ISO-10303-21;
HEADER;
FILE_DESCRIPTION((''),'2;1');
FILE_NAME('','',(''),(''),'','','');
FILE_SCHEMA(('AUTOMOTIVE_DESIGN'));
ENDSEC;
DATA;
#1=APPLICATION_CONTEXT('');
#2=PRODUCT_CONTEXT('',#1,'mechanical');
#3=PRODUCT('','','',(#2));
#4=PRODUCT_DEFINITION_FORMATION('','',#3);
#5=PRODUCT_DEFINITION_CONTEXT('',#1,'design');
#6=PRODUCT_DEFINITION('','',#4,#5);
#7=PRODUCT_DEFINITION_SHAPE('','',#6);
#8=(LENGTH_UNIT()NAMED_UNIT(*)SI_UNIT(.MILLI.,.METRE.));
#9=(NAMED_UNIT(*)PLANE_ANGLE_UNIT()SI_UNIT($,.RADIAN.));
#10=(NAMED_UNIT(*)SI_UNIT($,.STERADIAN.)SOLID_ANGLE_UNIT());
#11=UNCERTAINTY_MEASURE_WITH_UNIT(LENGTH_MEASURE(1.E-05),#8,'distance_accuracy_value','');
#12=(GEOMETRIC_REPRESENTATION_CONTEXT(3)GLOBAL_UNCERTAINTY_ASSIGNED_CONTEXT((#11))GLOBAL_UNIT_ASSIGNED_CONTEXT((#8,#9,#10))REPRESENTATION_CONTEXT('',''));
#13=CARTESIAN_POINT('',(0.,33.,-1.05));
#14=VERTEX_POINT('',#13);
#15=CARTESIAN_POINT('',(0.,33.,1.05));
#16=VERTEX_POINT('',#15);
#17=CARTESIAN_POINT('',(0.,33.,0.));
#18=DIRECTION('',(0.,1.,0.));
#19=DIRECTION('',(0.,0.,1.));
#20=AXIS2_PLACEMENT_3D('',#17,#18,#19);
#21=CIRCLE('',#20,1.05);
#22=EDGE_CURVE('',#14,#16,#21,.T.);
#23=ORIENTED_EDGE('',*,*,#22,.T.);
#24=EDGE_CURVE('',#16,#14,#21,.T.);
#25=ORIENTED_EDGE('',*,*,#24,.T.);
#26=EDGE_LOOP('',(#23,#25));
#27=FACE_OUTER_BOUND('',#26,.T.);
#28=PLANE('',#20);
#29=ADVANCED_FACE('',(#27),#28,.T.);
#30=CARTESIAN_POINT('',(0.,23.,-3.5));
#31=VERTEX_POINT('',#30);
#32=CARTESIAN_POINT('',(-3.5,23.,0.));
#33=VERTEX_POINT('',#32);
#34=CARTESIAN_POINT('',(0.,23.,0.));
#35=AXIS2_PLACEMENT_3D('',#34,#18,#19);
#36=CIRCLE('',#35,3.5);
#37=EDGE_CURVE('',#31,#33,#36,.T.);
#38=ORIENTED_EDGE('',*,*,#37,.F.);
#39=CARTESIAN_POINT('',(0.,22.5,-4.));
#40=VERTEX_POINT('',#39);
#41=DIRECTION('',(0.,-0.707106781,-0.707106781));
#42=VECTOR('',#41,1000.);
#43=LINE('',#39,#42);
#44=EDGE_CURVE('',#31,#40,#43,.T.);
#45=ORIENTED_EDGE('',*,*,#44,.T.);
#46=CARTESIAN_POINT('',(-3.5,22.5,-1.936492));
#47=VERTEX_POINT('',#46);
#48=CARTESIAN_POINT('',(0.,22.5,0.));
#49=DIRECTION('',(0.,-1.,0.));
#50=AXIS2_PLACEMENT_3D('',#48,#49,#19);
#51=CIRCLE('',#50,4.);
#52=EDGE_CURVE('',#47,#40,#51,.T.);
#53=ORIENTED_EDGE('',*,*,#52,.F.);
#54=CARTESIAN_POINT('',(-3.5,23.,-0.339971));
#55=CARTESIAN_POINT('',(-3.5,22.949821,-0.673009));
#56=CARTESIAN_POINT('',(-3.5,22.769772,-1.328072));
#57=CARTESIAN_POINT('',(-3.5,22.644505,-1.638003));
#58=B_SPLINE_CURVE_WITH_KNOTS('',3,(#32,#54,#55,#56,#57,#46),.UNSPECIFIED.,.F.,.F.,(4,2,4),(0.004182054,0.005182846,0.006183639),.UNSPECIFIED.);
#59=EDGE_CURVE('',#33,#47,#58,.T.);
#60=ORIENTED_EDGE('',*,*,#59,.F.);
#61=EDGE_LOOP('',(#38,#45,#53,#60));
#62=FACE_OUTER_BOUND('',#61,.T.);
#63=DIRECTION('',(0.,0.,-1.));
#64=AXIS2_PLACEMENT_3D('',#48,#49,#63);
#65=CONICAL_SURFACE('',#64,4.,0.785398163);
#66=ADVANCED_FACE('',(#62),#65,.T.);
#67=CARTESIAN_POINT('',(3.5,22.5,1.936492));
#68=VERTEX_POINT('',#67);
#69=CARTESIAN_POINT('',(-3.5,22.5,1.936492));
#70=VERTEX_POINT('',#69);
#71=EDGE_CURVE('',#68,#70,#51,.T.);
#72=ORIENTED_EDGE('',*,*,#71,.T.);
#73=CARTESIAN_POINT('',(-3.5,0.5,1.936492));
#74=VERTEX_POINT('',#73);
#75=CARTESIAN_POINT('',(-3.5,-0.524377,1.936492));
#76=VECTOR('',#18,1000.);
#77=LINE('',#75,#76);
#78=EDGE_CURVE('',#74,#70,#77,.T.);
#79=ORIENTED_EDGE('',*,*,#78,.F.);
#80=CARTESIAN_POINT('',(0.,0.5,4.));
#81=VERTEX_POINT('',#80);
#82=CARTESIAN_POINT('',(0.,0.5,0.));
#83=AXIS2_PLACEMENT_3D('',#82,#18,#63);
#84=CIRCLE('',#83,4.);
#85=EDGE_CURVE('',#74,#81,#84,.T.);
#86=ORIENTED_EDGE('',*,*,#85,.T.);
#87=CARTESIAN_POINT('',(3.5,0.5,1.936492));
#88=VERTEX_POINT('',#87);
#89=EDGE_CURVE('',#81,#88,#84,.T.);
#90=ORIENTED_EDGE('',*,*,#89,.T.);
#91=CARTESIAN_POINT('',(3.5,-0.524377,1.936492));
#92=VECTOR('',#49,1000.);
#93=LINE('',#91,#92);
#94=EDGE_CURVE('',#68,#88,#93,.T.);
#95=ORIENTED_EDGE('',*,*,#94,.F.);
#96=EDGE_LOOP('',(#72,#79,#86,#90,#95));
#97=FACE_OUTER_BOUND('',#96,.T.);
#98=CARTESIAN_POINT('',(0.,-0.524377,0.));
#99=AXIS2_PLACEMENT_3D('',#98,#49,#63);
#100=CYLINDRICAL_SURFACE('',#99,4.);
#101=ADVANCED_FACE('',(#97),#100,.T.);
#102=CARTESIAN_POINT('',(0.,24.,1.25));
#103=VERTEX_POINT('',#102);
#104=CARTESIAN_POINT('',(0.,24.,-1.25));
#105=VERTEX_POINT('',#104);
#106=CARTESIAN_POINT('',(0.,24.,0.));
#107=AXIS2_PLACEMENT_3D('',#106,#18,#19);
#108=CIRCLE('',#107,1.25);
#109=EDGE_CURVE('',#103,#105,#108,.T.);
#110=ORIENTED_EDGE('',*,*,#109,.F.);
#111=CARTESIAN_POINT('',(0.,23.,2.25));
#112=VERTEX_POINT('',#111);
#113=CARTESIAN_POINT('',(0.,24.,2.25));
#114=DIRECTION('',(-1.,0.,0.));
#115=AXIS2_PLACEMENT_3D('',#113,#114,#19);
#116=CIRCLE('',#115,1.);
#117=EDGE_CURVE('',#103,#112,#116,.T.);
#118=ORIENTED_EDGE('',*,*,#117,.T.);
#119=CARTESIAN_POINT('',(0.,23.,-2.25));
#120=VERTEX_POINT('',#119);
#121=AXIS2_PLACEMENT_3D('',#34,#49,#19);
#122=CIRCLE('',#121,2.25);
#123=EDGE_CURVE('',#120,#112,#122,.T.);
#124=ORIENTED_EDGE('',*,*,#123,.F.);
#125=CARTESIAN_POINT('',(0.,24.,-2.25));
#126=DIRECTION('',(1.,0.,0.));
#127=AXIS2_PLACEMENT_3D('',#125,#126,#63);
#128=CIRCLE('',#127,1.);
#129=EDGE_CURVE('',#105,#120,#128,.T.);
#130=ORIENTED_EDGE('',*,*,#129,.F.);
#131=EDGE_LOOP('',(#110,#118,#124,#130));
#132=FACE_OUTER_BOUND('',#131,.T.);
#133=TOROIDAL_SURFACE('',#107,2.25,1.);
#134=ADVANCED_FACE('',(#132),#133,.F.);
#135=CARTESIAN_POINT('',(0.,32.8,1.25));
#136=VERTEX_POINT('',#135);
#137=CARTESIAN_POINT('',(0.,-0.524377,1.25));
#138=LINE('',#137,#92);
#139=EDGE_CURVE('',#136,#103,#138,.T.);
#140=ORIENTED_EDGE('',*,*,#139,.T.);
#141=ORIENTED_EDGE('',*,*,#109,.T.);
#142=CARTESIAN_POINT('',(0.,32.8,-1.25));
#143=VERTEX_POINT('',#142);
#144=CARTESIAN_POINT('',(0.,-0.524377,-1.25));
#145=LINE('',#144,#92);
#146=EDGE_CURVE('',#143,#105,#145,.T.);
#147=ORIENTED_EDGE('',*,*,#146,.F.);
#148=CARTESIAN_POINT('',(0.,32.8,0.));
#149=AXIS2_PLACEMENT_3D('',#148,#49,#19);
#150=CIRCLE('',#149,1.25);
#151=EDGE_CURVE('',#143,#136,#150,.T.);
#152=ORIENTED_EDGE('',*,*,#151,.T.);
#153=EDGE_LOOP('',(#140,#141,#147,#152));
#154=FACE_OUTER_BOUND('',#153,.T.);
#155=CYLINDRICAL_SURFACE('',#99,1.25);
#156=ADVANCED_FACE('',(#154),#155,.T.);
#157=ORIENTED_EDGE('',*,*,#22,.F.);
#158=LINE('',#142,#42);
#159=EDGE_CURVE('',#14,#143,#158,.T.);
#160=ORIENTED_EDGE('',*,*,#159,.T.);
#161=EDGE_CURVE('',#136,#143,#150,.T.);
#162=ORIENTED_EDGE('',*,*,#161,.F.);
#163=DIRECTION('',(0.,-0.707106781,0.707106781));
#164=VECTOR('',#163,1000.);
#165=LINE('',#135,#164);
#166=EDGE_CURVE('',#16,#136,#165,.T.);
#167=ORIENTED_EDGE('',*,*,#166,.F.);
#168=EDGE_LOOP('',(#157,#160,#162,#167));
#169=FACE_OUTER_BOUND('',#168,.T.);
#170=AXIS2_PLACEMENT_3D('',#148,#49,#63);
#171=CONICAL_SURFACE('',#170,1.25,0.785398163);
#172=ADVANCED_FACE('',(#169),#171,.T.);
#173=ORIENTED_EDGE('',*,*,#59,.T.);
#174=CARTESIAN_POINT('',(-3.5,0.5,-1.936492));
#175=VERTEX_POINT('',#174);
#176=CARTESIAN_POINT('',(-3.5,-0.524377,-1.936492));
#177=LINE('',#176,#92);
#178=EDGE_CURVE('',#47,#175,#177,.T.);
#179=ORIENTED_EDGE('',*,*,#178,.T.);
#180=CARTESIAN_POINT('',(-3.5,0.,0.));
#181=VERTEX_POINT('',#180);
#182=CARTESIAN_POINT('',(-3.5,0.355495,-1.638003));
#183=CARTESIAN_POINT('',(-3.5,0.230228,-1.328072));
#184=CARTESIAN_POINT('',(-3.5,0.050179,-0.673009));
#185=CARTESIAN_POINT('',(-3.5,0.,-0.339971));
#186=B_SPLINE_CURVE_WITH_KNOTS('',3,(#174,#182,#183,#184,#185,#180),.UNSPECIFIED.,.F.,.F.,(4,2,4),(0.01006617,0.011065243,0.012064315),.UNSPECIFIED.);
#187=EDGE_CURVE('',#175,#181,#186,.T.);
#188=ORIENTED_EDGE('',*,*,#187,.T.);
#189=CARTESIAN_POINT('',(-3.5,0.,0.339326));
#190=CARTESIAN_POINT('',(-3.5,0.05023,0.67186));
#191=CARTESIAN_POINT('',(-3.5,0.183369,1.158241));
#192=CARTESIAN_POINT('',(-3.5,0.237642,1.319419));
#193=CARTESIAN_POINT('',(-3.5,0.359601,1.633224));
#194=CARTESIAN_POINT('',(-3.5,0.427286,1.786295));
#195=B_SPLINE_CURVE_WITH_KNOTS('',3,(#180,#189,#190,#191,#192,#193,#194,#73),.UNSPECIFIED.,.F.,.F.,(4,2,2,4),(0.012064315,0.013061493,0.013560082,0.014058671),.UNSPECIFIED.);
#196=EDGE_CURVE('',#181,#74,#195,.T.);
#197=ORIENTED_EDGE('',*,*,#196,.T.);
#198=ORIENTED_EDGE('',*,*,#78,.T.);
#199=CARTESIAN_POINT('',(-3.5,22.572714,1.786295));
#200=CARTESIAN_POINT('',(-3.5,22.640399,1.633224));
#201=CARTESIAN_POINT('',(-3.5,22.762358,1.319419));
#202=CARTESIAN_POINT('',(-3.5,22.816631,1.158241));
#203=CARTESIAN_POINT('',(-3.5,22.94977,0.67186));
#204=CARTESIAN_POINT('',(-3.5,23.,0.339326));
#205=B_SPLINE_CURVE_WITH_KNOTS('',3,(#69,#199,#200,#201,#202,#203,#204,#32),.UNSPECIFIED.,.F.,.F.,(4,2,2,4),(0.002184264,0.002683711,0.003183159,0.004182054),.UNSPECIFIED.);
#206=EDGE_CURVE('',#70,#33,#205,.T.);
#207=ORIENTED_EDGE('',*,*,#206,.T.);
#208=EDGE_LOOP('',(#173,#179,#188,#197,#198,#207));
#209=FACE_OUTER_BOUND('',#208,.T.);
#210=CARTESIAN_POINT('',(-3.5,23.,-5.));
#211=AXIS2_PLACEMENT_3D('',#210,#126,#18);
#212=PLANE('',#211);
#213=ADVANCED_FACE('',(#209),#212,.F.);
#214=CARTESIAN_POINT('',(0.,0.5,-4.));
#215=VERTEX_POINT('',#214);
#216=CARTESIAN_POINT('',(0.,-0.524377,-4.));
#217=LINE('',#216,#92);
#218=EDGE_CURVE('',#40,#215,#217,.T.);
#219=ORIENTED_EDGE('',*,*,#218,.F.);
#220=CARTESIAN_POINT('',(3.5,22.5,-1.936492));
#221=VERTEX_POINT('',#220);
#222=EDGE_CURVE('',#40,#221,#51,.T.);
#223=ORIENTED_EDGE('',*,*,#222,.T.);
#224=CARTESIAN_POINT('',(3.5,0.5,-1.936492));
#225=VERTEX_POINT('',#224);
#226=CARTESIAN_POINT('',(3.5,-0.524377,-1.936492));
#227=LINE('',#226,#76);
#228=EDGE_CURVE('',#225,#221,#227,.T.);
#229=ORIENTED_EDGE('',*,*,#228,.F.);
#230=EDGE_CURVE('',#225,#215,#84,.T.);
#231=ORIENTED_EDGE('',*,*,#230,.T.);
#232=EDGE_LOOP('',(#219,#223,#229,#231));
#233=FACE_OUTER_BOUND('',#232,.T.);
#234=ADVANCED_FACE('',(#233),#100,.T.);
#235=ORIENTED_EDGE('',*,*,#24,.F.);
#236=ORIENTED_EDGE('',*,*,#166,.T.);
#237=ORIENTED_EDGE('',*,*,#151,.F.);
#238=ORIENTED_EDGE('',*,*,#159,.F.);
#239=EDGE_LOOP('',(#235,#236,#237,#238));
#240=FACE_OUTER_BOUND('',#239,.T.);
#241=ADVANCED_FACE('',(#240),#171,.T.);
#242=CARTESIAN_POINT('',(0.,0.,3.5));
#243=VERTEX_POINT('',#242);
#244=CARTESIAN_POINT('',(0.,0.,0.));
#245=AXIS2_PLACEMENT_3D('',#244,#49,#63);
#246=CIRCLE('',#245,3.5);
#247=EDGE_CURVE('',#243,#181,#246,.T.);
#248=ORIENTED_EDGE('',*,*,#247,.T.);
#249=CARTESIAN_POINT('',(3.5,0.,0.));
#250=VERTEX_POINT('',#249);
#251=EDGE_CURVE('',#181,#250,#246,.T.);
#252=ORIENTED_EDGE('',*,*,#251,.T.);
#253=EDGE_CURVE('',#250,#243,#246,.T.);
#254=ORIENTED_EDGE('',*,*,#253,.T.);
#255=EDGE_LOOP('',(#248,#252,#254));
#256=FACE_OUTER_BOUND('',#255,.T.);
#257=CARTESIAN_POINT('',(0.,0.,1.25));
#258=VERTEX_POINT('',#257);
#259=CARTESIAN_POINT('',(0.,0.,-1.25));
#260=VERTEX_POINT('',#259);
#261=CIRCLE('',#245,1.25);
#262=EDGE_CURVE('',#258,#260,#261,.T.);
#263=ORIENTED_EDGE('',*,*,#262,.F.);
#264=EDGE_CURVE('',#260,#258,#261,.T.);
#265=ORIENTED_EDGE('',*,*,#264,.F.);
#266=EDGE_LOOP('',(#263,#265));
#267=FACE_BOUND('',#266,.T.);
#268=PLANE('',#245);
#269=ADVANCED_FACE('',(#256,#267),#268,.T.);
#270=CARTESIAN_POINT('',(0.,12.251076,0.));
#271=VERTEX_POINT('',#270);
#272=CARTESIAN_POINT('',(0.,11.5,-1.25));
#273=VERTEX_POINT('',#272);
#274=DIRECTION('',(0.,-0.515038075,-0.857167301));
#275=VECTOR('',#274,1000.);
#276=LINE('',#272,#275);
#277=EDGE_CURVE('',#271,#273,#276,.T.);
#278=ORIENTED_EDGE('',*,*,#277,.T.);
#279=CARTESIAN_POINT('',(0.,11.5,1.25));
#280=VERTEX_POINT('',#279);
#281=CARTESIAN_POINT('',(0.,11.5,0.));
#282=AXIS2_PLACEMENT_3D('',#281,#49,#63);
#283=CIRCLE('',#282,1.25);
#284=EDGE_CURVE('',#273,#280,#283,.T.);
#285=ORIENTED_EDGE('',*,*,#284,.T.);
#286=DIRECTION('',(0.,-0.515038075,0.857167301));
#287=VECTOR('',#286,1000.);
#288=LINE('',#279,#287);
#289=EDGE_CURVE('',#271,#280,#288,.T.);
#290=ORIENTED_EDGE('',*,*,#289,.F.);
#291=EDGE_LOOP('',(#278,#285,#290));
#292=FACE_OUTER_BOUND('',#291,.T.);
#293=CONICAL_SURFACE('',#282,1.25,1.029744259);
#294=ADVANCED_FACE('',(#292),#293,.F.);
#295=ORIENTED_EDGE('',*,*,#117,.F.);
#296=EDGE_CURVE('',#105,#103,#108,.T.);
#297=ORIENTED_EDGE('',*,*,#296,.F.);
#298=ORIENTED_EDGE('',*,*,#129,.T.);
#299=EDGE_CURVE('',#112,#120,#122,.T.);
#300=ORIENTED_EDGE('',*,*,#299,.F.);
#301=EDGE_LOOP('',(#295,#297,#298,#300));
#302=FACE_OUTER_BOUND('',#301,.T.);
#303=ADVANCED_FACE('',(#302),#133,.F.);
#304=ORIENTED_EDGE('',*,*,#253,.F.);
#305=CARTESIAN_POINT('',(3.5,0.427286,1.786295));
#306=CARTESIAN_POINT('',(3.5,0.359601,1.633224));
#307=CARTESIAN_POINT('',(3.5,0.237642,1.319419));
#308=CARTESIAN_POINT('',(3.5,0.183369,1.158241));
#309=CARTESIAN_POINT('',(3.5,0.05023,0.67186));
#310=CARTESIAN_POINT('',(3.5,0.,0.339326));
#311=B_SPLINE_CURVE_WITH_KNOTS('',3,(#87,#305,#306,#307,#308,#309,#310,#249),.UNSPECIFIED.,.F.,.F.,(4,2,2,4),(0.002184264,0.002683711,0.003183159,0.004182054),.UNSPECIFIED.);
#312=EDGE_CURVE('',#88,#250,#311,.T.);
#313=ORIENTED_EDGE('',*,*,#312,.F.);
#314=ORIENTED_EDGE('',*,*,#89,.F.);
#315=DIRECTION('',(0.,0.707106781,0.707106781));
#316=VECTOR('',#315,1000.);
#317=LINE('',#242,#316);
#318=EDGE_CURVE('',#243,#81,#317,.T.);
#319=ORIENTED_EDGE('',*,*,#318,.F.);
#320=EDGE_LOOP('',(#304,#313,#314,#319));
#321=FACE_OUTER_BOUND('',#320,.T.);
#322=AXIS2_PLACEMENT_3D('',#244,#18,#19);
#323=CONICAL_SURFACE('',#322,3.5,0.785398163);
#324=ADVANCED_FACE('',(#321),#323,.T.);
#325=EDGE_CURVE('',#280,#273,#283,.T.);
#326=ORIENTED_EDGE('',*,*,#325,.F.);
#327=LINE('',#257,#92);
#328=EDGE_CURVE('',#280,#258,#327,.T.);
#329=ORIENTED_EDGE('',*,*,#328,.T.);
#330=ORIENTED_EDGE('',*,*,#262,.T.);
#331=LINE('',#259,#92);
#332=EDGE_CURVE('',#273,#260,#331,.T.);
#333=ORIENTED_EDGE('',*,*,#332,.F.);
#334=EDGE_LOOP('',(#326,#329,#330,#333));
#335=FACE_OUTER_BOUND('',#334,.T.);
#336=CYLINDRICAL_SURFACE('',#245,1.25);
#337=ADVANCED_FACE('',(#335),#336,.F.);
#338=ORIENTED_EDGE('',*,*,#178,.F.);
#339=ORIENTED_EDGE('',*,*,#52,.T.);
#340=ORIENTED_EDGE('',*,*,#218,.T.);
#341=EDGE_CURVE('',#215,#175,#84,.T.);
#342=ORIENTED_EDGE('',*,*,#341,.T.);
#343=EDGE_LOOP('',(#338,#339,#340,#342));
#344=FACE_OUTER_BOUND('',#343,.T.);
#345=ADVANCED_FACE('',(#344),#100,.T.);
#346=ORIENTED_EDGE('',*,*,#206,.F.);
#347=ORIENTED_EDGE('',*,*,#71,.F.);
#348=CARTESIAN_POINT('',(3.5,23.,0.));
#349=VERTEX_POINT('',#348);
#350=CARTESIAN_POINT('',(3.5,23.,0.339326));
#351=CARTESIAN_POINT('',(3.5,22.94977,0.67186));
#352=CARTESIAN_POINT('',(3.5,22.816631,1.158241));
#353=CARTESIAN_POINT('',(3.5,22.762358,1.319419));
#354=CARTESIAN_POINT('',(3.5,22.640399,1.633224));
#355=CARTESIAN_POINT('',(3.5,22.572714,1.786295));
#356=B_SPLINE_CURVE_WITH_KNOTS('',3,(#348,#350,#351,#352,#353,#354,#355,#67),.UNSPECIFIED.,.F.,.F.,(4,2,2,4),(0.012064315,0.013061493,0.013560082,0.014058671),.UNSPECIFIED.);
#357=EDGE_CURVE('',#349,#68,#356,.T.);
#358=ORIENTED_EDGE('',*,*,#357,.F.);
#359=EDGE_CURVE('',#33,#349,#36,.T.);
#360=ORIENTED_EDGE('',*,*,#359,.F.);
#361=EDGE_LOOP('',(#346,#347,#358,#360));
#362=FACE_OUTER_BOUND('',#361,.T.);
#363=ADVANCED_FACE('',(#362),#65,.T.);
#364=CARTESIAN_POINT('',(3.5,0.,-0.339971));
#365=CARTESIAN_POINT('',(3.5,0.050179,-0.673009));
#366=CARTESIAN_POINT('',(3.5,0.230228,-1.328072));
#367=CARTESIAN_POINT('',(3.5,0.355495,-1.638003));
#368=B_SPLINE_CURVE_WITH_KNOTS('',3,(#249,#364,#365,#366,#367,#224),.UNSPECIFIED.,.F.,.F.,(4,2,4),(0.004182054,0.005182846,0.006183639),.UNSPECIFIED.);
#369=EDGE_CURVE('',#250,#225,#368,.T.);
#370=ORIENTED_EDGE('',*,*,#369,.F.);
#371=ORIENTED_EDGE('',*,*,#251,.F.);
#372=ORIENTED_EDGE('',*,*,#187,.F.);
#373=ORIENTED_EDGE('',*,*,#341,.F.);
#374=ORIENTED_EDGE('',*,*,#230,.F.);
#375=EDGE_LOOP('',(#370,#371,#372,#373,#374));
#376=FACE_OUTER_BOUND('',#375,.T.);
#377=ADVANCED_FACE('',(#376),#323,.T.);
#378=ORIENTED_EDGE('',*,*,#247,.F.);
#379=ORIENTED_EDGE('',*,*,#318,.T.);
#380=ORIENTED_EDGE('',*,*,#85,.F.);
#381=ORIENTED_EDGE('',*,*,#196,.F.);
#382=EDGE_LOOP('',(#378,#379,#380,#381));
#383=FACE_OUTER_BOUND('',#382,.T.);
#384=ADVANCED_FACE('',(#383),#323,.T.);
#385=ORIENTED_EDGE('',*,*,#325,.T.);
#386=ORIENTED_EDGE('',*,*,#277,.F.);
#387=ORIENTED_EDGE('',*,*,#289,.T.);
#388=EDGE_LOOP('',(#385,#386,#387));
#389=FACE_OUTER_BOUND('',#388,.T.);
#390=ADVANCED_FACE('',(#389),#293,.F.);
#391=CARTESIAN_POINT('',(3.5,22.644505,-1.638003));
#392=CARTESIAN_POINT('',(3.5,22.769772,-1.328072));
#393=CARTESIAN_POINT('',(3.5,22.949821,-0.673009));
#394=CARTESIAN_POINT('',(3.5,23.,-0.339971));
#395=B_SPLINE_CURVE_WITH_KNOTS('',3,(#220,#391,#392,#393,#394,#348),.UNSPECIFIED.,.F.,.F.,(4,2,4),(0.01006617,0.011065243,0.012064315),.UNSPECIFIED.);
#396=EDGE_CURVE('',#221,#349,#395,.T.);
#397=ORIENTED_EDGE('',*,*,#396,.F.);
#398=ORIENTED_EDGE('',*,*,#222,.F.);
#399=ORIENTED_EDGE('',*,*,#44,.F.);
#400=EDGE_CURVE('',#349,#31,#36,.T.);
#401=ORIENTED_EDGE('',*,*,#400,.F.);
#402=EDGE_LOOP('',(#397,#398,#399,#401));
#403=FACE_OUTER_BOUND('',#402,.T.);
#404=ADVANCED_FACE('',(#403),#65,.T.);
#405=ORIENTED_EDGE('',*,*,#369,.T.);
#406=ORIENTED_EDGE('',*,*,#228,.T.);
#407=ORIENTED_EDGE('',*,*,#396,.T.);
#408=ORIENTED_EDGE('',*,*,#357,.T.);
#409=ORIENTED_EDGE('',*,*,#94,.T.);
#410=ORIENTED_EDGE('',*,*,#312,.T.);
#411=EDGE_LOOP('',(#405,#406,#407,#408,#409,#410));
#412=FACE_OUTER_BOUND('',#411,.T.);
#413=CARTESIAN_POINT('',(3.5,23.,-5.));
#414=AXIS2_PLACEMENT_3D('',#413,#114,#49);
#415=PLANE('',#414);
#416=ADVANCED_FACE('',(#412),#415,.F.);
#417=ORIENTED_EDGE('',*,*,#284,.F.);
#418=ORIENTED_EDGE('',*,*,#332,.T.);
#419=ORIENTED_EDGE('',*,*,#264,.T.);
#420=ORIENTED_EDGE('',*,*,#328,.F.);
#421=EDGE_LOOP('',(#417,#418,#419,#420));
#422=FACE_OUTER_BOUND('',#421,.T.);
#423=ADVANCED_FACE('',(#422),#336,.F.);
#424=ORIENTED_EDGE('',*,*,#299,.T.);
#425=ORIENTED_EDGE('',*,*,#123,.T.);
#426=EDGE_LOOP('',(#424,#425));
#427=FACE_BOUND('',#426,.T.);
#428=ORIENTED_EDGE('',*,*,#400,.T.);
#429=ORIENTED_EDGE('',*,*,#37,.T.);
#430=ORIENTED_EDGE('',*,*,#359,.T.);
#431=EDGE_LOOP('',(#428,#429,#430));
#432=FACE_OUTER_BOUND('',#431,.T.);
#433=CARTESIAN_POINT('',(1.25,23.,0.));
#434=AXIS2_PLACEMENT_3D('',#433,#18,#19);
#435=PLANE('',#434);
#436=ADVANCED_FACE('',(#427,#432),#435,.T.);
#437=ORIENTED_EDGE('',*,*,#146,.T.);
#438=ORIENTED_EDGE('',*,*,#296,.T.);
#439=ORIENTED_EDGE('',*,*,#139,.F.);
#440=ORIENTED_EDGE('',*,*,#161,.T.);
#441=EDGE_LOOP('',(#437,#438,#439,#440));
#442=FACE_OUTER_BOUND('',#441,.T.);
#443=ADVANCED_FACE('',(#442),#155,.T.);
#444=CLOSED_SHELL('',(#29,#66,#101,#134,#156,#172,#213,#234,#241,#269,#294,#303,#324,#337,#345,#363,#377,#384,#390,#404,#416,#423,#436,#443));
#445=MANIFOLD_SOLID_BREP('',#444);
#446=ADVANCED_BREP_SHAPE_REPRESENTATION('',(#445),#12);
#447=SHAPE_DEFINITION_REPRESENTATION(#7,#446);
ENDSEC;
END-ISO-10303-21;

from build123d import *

# Parameters (mm, degrees)
HOLE_WIZARD_M3_1_D     = 2.5
HOLE_WIZARD_M3_1_DEPTH = 11.5
HOLE_WIZARD_M3_1_TIP   = 0.751075774
CHAMFER_1_SIZE         = 0.5
FILLET_1_R             = 1
SKETCH_4_W             = 0.5
SKETCH_4_H             = 23
CUT_EXTRUDE_1_DEPTH    = 5
CHAMFER_2_SIZE         = 0.2


with BuildPart() as part:
    # 草图1 → 旋转1 (revolve)
    with BuildSketch(Plane.XY, mode=Mode.PRIVATE) as revolve_1_sk:
        Polygon((1.25, 33), (1.25, 23), (4, 23), (4, 0), (0, 0), (0, 33), align=None)
    revolve(revolve_1_sk.sketch.rotate(Axis((0, -0.524377328, 0), (0, 1, 0)), 90), axis=Axis((0, -0.524377328, 0), (0, 1, 0)))

    # M3 螺纹孔1
    with Locations(Plane(origin=(0, 0, 0), x_dir=(-1, 0, 0), z_dir=(0, -1, 0))):
        with Locations((0, 0)):
            Hole(HOLE_WIZARD_M3_1_D / 2, depth=HOLE_WIZARD_M3_1_DEPTH)
            with Locations((0, 0, -(HOLE_WIZARD_M3_1_DEPTH + HOLE_WIZARD_M3_1_TIP / 2))):  # 118° drill point
                Cone(0, HOLE_WIZARD_M3_1_D / 2, HOLE_WIZARD_M3_1_TIP, mode=Mode.SUBTRACT)

    # 倒角1
    chamfer_1_edges = [part.edges().sort_by_distance(p)[0] for p in [
        (0, 0, 4),
        (0, 23, 4),
    ]]
    chamfer(chamfer_1_edges, length=CHAMFER_1_SIZE)

    # 圆角1
    fillet_1_edges = [part.edges().sort_by_distance(p)[0] for p in [
        (0, 23, 1.25),
    ]]
    fillet(fillet_1_edges, radius=FILLET_1_R)

    # 草图4 → 切除-拉伸1 (cut, symmetric)
    with BuildSketch(Plane.XY):
        with Locations((3.75, 11.5)):
            Rectangle(SKETCH_4_W, SKETCH_4_H)
        with Locations((-3.75, 11.5)):
            Rectangle(SKETCH_4_W, SKETCH_4_H)
    extrude(amount=CUT_EXTRUDE_1_DEPTH, both=True, mode=Mode.SUBTRACT)

    # 倒角2
    chamfer_2_edges = [part.edges().sort_by_distance(p)[0] for p in [
        (0, 33, 1.25),
    ]]
    chamfer(chamfer_2_edges, length=CHAMFER_2_SIZE)


solid = part.part
